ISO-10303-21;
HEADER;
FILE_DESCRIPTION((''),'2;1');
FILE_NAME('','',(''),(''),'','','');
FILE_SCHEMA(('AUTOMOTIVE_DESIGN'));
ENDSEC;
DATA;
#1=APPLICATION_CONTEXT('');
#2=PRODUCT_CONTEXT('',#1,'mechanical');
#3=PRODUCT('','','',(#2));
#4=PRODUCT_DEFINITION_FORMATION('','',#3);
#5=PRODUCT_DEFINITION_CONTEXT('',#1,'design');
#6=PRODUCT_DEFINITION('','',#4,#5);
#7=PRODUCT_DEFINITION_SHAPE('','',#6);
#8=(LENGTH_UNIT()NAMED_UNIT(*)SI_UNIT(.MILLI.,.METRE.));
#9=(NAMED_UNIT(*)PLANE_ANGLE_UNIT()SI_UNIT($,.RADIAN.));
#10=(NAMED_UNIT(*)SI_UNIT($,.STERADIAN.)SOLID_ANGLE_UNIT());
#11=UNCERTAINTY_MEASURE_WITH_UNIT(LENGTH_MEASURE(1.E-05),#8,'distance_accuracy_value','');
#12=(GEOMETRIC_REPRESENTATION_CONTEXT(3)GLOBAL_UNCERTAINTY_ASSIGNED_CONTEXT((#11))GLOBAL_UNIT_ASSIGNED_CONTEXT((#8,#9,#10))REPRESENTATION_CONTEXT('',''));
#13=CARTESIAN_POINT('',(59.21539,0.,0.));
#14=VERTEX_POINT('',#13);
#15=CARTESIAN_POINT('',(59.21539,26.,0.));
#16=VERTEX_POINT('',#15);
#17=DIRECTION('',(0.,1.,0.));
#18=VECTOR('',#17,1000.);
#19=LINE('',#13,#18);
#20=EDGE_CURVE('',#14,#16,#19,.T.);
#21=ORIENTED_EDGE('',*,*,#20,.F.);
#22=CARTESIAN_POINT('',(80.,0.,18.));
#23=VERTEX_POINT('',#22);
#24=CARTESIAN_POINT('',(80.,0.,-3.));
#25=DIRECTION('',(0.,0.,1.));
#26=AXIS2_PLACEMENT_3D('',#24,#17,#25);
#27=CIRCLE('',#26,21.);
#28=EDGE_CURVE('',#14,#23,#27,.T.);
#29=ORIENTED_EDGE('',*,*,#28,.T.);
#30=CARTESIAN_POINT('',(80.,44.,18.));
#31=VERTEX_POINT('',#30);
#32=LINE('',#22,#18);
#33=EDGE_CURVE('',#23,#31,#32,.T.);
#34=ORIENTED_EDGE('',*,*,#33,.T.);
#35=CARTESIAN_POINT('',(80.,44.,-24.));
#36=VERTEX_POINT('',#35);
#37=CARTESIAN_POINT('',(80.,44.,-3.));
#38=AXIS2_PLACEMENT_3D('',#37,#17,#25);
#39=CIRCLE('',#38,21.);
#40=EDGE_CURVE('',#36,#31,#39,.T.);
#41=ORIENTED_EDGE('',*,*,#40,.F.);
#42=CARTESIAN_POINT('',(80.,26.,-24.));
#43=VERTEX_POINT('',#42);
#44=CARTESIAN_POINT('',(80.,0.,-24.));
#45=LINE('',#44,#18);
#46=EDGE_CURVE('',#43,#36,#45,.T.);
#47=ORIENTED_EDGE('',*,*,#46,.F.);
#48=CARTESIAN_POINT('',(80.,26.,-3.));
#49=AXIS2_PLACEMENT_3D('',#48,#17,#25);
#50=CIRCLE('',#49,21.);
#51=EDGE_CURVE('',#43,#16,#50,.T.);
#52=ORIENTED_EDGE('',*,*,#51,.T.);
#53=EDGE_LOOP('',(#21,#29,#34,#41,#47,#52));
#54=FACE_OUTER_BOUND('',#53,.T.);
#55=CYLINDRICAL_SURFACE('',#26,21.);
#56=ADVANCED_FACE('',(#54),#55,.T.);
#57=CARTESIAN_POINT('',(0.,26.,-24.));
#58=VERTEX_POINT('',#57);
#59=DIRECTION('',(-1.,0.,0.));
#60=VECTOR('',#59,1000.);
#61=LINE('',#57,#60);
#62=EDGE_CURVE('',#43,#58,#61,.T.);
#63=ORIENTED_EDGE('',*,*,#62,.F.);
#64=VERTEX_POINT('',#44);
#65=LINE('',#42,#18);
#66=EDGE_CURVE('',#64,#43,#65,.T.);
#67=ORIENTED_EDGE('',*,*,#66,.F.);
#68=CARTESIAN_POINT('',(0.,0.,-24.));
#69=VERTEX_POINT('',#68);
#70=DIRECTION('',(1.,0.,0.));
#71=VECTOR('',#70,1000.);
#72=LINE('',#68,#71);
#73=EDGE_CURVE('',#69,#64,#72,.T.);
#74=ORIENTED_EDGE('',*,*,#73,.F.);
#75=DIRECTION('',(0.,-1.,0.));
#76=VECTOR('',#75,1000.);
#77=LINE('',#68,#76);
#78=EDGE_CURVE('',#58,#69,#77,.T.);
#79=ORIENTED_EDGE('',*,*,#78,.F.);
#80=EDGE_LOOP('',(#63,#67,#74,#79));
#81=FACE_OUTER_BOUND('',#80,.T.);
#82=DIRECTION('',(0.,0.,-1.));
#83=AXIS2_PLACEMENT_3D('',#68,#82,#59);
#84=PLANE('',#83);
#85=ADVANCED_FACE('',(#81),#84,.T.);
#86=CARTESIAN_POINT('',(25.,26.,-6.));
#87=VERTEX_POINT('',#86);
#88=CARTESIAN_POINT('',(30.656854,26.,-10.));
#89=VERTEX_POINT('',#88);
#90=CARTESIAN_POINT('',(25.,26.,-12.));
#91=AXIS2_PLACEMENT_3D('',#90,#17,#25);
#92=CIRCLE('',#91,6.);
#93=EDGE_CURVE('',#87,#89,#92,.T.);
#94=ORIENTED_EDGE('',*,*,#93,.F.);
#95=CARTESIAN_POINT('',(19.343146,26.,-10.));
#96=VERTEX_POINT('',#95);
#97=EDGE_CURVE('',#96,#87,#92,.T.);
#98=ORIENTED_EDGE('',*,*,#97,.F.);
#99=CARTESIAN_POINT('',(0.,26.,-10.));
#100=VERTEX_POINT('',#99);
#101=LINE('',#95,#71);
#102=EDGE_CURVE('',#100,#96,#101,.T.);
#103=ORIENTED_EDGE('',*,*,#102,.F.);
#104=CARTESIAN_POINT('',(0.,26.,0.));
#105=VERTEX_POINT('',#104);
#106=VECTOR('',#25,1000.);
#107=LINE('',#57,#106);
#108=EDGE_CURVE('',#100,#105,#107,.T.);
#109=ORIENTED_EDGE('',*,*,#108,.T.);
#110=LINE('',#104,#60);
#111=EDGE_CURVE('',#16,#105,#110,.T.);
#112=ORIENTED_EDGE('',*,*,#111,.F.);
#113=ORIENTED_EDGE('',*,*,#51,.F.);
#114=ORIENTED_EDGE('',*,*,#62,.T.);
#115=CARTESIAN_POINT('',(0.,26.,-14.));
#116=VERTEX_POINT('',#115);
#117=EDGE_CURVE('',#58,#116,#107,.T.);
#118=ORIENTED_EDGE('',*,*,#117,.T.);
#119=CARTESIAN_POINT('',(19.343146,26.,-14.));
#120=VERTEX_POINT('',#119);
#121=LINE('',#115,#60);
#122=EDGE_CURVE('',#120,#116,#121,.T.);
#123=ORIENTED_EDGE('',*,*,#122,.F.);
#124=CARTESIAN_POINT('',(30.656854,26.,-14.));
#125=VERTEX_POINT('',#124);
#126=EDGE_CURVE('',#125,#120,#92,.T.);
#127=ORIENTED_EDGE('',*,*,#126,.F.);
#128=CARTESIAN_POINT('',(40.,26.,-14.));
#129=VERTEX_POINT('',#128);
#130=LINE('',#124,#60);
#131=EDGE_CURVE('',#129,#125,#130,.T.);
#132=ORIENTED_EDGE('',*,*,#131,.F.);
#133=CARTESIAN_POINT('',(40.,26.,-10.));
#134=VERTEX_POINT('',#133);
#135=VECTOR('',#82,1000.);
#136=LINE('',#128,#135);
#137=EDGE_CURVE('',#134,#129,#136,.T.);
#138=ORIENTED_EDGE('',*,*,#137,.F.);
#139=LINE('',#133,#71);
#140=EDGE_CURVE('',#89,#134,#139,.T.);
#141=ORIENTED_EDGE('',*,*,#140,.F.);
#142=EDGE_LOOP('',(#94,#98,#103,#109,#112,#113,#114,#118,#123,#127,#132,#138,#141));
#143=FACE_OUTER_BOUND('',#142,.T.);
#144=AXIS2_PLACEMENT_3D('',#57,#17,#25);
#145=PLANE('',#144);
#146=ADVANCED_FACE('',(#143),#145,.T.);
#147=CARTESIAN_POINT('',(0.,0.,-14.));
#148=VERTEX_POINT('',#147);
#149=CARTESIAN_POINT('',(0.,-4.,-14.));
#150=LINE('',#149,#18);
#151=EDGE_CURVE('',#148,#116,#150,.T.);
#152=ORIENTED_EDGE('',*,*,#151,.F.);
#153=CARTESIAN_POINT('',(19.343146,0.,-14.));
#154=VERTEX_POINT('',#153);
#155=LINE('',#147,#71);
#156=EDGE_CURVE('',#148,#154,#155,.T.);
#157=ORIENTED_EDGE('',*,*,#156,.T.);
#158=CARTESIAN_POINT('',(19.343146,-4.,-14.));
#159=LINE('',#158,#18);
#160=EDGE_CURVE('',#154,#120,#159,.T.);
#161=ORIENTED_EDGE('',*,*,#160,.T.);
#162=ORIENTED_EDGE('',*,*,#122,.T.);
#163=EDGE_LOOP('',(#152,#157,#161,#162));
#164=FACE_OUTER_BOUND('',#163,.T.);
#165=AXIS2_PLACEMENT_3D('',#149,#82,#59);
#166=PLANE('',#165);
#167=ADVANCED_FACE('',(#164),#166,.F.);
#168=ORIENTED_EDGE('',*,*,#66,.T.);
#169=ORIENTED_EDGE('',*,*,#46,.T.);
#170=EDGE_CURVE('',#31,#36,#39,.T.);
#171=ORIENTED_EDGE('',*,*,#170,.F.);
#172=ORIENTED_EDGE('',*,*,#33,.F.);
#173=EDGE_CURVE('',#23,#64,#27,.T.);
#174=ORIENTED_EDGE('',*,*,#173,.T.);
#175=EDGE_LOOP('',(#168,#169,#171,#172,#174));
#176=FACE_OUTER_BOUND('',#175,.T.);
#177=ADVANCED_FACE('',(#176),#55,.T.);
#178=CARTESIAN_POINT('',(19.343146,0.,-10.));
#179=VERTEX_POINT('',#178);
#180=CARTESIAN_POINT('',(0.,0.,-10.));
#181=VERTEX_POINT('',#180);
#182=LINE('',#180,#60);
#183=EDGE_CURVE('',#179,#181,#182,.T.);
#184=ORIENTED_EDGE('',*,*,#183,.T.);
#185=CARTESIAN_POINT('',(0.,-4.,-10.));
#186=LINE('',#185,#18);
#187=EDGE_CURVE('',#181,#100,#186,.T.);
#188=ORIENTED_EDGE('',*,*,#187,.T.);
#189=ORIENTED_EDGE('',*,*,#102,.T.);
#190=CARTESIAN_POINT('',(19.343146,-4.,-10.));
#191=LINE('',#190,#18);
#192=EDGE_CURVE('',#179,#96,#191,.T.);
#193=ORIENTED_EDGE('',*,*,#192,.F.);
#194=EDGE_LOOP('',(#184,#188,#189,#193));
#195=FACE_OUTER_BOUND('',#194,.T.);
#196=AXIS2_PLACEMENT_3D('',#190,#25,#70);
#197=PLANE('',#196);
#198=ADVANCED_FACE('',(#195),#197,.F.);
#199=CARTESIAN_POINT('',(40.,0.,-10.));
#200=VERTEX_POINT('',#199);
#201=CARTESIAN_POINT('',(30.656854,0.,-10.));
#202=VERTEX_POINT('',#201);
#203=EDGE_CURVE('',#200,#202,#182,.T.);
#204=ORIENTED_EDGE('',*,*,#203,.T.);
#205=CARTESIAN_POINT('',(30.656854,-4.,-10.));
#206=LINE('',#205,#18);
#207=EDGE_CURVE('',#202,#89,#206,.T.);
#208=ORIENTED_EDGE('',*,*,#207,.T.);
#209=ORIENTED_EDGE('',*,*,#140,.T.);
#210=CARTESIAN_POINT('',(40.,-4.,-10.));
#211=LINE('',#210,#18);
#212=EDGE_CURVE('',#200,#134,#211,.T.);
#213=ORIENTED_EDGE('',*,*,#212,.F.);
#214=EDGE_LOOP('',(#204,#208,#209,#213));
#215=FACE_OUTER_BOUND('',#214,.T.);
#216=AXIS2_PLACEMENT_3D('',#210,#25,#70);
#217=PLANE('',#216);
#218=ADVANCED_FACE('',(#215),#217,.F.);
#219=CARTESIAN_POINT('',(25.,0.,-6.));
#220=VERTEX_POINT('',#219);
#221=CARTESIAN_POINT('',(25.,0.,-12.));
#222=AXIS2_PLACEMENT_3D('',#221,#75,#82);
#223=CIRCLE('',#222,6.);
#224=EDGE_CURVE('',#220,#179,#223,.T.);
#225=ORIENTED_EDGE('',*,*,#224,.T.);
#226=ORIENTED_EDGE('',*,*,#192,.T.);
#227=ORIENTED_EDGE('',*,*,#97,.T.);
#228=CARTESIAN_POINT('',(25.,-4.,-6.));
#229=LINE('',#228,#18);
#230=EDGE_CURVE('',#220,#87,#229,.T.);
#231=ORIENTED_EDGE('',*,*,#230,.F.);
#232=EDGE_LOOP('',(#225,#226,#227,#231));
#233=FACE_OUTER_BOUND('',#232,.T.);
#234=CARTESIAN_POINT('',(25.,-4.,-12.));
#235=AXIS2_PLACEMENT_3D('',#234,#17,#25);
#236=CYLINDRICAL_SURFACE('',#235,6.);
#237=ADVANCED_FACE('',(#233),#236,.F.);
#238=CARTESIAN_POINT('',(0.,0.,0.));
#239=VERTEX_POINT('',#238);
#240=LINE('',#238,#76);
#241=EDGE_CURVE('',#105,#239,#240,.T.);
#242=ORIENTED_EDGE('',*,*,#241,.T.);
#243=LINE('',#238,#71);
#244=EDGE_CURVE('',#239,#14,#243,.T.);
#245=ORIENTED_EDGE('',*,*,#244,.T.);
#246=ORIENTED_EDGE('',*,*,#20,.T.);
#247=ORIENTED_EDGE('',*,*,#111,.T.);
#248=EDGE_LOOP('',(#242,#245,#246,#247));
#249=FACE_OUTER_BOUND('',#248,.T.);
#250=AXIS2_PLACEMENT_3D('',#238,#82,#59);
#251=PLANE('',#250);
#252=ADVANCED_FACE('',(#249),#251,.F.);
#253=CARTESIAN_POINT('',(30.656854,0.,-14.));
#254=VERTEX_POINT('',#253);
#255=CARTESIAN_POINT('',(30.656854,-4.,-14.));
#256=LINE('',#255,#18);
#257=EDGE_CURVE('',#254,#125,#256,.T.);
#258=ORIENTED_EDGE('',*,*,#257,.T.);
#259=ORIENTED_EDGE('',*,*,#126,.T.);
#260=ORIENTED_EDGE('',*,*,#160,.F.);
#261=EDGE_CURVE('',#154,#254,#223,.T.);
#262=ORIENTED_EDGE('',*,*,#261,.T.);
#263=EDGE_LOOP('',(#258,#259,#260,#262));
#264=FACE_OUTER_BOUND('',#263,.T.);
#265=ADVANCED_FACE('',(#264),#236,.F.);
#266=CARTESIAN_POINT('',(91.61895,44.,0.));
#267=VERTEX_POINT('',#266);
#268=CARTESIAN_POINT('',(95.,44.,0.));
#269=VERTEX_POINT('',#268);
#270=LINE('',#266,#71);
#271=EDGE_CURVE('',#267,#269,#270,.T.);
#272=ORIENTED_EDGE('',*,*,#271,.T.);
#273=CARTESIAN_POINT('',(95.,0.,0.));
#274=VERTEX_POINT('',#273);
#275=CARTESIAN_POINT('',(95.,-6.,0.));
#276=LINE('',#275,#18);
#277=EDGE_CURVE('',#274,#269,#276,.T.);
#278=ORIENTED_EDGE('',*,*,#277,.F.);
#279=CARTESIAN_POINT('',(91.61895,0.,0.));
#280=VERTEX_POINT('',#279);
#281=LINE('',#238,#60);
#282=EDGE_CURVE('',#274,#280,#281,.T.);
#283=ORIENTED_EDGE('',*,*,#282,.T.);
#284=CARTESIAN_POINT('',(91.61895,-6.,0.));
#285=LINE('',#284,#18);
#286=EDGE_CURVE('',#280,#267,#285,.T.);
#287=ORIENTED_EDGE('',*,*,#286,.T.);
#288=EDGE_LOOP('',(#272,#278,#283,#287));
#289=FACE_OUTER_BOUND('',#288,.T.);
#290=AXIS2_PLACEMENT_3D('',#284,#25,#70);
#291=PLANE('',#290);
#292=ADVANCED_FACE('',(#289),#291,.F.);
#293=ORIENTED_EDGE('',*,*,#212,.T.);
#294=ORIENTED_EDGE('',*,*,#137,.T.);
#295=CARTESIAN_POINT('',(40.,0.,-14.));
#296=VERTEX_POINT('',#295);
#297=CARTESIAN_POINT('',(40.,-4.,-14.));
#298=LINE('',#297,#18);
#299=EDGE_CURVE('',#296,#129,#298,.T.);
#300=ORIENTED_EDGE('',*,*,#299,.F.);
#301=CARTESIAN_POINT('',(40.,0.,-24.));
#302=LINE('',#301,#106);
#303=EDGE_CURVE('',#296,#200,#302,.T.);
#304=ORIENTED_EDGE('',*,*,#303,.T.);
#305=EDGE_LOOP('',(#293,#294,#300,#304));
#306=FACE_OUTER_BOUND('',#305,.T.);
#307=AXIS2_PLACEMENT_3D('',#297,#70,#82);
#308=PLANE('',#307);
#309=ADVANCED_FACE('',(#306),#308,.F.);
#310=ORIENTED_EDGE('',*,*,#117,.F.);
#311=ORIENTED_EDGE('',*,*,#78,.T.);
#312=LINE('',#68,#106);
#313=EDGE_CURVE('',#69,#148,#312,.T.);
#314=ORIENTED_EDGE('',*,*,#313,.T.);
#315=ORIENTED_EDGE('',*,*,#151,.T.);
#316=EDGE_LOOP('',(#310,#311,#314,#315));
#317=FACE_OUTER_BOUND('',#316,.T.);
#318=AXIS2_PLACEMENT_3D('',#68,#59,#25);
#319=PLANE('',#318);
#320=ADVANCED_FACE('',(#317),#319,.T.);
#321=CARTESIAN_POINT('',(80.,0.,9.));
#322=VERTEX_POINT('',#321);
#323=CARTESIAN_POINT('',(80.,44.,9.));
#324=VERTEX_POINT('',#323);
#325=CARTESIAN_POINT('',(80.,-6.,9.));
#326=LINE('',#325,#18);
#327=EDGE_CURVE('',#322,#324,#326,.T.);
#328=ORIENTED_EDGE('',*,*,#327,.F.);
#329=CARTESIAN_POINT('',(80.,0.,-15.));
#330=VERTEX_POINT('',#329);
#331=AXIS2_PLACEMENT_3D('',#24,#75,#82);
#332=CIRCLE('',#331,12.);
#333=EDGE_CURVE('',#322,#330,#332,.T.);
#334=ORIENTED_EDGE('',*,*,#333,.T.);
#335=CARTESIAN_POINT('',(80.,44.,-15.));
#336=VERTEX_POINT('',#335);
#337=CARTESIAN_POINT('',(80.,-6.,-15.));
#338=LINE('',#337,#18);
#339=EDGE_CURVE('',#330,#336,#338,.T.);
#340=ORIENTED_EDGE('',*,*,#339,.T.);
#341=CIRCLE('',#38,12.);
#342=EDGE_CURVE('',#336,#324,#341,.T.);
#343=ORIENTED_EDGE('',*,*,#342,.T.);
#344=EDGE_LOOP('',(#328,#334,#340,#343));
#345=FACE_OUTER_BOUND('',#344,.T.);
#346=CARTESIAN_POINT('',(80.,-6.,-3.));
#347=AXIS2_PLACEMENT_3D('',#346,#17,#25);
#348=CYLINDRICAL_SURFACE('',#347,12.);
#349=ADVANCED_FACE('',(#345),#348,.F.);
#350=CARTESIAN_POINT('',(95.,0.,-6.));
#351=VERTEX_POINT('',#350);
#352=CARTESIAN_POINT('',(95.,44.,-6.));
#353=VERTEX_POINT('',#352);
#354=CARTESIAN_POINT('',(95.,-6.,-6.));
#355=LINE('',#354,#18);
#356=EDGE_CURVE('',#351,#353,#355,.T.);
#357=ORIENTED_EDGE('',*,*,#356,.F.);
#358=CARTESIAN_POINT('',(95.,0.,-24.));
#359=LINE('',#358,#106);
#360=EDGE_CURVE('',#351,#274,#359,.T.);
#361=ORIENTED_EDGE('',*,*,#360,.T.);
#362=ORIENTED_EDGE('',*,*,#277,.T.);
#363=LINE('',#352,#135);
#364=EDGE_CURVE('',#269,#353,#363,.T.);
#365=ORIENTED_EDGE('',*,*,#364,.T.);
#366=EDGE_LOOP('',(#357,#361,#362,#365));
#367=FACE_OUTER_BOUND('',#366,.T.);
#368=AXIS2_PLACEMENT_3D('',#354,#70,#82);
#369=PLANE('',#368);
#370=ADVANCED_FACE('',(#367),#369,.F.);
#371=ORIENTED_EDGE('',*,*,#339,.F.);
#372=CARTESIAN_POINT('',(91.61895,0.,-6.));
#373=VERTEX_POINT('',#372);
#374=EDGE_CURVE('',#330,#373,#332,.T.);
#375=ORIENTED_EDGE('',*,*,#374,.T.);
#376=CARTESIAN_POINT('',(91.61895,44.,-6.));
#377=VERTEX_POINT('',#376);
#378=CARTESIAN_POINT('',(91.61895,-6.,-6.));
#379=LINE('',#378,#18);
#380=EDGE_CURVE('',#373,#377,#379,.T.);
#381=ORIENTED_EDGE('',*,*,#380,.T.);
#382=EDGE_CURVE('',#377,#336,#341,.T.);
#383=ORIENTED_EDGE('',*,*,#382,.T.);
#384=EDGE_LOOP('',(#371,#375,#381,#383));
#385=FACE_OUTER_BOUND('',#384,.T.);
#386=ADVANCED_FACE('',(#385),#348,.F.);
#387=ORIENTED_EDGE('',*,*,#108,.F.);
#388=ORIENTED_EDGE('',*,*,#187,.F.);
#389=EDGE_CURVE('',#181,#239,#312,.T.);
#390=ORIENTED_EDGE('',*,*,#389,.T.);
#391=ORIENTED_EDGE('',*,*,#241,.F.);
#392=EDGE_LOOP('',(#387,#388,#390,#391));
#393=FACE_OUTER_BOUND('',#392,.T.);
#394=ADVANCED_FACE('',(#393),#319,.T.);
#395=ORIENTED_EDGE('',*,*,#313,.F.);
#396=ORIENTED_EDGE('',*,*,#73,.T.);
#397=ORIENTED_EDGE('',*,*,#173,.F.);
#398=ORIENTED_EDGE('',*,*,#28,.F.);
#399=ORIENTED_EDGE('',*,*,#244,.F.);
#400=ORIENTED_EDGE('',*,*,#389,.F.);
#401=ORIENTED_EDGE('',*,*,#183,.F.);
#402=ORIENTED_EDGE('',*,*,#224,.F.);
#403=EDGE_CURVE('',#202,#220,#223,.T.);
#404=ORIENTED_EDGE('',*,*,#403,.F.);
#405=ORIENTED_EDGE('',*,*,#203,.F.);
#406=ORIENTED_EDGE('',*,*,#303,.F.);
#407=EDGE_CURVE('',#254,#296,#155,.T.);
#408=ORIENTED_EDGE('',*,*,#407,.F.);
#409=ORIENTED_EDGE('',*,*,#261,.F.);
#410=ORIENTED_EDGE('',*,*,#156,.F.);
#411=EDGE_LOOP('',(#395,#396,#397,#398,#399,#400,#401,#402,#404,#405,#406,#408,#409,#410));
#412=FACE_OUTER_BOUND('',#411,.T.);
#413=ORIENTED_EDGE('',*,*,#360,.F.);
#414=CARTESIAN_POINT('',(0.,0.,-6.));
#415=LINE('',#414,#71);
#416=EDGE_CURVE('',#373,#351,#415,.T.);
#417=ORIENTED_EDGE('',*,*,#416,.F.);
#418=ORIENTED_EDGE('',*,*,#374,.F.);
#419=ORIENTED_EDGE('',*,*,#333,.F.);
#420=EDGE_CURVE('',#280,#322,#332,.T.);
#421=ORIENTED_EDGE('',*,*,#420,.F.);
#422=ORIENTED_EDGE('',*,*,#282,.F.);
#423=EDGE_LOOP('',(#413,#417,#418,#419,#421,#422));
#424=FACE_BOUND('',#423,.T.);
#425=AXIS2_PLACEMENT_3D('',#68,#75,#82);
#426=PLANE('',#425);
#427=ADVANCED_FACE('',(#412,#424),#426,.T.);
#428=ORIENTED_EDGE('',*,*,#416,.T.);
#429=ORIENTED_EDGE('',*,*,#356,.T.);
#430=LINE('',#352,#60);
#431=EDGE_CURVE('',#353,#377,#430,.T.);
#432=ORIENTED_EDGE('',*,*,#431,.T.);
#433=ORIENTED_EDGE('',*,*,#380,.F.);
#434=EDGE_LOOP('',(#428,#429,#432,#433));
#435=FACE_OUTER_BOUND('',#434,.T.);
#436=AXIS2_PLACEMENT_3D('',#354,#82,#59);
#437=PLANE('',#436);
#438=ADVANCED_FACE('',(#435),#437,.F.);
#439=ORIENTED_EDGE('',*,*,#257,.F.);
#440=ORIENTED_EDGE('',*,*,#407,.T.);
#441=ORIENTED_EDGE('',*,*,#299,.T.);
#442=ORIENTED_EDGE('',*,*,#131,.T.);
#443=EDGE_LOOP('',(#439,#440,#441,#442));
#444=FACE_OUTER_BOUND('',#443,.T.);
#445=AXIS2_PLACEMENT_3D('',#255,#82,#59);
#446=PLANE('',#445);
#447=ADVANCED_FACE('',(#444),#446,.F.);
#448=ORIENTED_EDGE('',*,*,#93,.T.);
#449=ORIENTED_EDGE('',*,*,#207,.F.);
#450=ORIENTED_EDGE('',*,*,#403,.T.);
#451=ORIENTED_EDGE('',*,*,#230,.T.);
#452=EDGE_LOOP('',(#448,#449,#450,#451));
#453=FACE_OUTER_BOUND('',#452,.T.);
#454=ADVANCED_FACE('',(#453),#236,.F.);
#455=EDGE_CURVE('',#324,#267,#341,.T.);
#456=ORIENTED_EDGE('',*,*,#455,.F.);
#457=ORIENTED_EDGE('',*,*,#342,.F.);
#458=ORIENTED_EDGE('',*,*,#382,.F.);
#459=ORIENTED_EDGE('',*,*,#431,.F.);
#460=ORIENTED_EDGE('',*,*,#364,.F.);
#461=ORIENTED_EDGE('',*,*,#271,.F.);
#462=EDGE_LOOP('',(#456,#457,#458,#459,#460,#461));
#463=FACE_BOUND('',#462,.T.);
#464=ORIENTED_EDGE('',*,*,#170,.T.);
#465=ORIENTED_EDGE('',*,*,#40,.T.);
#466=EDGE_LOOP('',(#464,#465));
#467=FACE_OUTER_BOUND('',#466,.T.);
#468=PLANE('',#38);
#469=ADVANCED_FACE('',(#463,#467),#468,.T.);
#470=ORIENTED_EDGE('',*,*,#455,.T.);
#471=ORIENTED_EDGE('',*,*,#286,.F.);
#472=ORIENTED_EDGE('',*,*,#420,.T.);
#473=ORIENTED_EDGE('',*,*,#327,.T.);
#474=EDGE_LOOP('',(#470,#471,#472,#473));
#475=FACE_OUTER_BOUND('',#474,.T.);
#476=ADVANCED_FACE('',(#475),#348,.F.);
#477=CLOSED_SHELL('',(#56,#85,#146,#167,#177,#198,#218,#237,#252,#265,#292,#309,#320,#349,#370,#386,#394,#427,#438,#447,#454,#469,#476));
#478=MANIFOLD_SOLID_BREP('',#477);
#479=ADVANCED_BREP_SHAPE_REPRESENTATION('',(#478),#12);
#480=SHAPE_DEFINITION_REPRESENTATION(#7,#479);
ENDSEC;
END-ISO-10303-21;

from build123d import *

# Parameters (mm, degrees)
LEVER_ARM_PROFILE_W        = 80
LEVER_ARM_PROFILE_H        = 26
LEVER_ARM_80X26_DEPTH      = 24
HUB_PROFILE_42_R           = 21
HUB_BOSS_42_DEPTH          = 26
HUB_START                  = 18
HUB_EXTENSION_PROFILE_42_R = 21
HUB_EXTENSION_42_DEPTH     = 18
CLAMP_SPLIT_SLOT_DEPTH     = 30
KEYED_BORE_24_DEPTH        = 50


with BuildPart() as part:
    # Lever Arm Profile → Lever Arm 80x26 (new body)
    with BuildSketch(Plane.XY):
        with Locations((40, 13)):
            Rectangle(LEVER_ARM_PROFILE_W, LEVER_ARM_PROFILE_H)
    extrude(amount=-LEVER_ARM_80X26_DEPTH)

    # Hub Profile Ø42 → Hub Boss Ø42 (add)
    with BuildSketch(Plane(origin=(0, 26, 0), x_dir=(1, 0, 0), z_dir=(0, 1, 0))):
        with Locations((80, 3)):
            Circle(HUB_PROFILE_42_R)
    extrude(amount=-HUB_BOSS_42_DEPTH)

    # Hub Extension Profile Ø42 → Hub Extension Ø42 (add)
    with BuildSketch(Plane(origin=(0, 26, 0), x_dir=(1, 0, 0), z_dir=(0, 1, 0)).offset(HUB_START)):
        with Locations(Location((80, 3, 0), (0, 0, 270))):
            Circle(HUB_EXTENSION_PROFILE_42_R)
    extrude(amount=-HUB_EXTENSION_42_DEPTH)

    # Clamp Slot Profile → Clamp Split Slot (cut)
    with BuildSketch(Plane(origin=(0, 26, 0), x_dir=(1, 0, 0), z_dir=(0, 1, 0))):
        with BuildLine():
            Line((0, 14), (0, 10))
            Line((0, 10), (19.343145751, 10))
            ThreePointArc((19.343145751, 10), (25, 6), (30.656854249, 10))
            Line((30.656854249, 10), (40, 10))
            Line((40, 10), (40, 14))
            Line((40, 14), (30.656854249, 14))
            ThreePointArc((30.656854249, 14), (25, 18), (19.343145751, 14))
            Line((19.343145751, 14), (0, 14))
        make_face()
    extrude(amount=-CLAMP_SPLIT_SLOT_DEPTH, mode=Mode.SUBTRACT)

    # Keyed Bore Profile → Keyed Bore Ø24 (cut)
    with BuildSketch(Plane(origin=(0, 44, 0), x_dir=(1, 0, 0), z_dir=(0, 1, 0))):
        with BuildLine():
            Line((95, 6), (91.618950039, 6))
            ThreePointArc((91.618950039, 6), (68, 3), (91.618950039, 0))
            Line((91.618950039, 0), (95, 0))
            Line((95, 0), (95, 6))
        make_face()
    extrude(amount=-KEYED_BORE_24_DEPTH, mode=Mode.SUBTRACT)


solid = part.part
